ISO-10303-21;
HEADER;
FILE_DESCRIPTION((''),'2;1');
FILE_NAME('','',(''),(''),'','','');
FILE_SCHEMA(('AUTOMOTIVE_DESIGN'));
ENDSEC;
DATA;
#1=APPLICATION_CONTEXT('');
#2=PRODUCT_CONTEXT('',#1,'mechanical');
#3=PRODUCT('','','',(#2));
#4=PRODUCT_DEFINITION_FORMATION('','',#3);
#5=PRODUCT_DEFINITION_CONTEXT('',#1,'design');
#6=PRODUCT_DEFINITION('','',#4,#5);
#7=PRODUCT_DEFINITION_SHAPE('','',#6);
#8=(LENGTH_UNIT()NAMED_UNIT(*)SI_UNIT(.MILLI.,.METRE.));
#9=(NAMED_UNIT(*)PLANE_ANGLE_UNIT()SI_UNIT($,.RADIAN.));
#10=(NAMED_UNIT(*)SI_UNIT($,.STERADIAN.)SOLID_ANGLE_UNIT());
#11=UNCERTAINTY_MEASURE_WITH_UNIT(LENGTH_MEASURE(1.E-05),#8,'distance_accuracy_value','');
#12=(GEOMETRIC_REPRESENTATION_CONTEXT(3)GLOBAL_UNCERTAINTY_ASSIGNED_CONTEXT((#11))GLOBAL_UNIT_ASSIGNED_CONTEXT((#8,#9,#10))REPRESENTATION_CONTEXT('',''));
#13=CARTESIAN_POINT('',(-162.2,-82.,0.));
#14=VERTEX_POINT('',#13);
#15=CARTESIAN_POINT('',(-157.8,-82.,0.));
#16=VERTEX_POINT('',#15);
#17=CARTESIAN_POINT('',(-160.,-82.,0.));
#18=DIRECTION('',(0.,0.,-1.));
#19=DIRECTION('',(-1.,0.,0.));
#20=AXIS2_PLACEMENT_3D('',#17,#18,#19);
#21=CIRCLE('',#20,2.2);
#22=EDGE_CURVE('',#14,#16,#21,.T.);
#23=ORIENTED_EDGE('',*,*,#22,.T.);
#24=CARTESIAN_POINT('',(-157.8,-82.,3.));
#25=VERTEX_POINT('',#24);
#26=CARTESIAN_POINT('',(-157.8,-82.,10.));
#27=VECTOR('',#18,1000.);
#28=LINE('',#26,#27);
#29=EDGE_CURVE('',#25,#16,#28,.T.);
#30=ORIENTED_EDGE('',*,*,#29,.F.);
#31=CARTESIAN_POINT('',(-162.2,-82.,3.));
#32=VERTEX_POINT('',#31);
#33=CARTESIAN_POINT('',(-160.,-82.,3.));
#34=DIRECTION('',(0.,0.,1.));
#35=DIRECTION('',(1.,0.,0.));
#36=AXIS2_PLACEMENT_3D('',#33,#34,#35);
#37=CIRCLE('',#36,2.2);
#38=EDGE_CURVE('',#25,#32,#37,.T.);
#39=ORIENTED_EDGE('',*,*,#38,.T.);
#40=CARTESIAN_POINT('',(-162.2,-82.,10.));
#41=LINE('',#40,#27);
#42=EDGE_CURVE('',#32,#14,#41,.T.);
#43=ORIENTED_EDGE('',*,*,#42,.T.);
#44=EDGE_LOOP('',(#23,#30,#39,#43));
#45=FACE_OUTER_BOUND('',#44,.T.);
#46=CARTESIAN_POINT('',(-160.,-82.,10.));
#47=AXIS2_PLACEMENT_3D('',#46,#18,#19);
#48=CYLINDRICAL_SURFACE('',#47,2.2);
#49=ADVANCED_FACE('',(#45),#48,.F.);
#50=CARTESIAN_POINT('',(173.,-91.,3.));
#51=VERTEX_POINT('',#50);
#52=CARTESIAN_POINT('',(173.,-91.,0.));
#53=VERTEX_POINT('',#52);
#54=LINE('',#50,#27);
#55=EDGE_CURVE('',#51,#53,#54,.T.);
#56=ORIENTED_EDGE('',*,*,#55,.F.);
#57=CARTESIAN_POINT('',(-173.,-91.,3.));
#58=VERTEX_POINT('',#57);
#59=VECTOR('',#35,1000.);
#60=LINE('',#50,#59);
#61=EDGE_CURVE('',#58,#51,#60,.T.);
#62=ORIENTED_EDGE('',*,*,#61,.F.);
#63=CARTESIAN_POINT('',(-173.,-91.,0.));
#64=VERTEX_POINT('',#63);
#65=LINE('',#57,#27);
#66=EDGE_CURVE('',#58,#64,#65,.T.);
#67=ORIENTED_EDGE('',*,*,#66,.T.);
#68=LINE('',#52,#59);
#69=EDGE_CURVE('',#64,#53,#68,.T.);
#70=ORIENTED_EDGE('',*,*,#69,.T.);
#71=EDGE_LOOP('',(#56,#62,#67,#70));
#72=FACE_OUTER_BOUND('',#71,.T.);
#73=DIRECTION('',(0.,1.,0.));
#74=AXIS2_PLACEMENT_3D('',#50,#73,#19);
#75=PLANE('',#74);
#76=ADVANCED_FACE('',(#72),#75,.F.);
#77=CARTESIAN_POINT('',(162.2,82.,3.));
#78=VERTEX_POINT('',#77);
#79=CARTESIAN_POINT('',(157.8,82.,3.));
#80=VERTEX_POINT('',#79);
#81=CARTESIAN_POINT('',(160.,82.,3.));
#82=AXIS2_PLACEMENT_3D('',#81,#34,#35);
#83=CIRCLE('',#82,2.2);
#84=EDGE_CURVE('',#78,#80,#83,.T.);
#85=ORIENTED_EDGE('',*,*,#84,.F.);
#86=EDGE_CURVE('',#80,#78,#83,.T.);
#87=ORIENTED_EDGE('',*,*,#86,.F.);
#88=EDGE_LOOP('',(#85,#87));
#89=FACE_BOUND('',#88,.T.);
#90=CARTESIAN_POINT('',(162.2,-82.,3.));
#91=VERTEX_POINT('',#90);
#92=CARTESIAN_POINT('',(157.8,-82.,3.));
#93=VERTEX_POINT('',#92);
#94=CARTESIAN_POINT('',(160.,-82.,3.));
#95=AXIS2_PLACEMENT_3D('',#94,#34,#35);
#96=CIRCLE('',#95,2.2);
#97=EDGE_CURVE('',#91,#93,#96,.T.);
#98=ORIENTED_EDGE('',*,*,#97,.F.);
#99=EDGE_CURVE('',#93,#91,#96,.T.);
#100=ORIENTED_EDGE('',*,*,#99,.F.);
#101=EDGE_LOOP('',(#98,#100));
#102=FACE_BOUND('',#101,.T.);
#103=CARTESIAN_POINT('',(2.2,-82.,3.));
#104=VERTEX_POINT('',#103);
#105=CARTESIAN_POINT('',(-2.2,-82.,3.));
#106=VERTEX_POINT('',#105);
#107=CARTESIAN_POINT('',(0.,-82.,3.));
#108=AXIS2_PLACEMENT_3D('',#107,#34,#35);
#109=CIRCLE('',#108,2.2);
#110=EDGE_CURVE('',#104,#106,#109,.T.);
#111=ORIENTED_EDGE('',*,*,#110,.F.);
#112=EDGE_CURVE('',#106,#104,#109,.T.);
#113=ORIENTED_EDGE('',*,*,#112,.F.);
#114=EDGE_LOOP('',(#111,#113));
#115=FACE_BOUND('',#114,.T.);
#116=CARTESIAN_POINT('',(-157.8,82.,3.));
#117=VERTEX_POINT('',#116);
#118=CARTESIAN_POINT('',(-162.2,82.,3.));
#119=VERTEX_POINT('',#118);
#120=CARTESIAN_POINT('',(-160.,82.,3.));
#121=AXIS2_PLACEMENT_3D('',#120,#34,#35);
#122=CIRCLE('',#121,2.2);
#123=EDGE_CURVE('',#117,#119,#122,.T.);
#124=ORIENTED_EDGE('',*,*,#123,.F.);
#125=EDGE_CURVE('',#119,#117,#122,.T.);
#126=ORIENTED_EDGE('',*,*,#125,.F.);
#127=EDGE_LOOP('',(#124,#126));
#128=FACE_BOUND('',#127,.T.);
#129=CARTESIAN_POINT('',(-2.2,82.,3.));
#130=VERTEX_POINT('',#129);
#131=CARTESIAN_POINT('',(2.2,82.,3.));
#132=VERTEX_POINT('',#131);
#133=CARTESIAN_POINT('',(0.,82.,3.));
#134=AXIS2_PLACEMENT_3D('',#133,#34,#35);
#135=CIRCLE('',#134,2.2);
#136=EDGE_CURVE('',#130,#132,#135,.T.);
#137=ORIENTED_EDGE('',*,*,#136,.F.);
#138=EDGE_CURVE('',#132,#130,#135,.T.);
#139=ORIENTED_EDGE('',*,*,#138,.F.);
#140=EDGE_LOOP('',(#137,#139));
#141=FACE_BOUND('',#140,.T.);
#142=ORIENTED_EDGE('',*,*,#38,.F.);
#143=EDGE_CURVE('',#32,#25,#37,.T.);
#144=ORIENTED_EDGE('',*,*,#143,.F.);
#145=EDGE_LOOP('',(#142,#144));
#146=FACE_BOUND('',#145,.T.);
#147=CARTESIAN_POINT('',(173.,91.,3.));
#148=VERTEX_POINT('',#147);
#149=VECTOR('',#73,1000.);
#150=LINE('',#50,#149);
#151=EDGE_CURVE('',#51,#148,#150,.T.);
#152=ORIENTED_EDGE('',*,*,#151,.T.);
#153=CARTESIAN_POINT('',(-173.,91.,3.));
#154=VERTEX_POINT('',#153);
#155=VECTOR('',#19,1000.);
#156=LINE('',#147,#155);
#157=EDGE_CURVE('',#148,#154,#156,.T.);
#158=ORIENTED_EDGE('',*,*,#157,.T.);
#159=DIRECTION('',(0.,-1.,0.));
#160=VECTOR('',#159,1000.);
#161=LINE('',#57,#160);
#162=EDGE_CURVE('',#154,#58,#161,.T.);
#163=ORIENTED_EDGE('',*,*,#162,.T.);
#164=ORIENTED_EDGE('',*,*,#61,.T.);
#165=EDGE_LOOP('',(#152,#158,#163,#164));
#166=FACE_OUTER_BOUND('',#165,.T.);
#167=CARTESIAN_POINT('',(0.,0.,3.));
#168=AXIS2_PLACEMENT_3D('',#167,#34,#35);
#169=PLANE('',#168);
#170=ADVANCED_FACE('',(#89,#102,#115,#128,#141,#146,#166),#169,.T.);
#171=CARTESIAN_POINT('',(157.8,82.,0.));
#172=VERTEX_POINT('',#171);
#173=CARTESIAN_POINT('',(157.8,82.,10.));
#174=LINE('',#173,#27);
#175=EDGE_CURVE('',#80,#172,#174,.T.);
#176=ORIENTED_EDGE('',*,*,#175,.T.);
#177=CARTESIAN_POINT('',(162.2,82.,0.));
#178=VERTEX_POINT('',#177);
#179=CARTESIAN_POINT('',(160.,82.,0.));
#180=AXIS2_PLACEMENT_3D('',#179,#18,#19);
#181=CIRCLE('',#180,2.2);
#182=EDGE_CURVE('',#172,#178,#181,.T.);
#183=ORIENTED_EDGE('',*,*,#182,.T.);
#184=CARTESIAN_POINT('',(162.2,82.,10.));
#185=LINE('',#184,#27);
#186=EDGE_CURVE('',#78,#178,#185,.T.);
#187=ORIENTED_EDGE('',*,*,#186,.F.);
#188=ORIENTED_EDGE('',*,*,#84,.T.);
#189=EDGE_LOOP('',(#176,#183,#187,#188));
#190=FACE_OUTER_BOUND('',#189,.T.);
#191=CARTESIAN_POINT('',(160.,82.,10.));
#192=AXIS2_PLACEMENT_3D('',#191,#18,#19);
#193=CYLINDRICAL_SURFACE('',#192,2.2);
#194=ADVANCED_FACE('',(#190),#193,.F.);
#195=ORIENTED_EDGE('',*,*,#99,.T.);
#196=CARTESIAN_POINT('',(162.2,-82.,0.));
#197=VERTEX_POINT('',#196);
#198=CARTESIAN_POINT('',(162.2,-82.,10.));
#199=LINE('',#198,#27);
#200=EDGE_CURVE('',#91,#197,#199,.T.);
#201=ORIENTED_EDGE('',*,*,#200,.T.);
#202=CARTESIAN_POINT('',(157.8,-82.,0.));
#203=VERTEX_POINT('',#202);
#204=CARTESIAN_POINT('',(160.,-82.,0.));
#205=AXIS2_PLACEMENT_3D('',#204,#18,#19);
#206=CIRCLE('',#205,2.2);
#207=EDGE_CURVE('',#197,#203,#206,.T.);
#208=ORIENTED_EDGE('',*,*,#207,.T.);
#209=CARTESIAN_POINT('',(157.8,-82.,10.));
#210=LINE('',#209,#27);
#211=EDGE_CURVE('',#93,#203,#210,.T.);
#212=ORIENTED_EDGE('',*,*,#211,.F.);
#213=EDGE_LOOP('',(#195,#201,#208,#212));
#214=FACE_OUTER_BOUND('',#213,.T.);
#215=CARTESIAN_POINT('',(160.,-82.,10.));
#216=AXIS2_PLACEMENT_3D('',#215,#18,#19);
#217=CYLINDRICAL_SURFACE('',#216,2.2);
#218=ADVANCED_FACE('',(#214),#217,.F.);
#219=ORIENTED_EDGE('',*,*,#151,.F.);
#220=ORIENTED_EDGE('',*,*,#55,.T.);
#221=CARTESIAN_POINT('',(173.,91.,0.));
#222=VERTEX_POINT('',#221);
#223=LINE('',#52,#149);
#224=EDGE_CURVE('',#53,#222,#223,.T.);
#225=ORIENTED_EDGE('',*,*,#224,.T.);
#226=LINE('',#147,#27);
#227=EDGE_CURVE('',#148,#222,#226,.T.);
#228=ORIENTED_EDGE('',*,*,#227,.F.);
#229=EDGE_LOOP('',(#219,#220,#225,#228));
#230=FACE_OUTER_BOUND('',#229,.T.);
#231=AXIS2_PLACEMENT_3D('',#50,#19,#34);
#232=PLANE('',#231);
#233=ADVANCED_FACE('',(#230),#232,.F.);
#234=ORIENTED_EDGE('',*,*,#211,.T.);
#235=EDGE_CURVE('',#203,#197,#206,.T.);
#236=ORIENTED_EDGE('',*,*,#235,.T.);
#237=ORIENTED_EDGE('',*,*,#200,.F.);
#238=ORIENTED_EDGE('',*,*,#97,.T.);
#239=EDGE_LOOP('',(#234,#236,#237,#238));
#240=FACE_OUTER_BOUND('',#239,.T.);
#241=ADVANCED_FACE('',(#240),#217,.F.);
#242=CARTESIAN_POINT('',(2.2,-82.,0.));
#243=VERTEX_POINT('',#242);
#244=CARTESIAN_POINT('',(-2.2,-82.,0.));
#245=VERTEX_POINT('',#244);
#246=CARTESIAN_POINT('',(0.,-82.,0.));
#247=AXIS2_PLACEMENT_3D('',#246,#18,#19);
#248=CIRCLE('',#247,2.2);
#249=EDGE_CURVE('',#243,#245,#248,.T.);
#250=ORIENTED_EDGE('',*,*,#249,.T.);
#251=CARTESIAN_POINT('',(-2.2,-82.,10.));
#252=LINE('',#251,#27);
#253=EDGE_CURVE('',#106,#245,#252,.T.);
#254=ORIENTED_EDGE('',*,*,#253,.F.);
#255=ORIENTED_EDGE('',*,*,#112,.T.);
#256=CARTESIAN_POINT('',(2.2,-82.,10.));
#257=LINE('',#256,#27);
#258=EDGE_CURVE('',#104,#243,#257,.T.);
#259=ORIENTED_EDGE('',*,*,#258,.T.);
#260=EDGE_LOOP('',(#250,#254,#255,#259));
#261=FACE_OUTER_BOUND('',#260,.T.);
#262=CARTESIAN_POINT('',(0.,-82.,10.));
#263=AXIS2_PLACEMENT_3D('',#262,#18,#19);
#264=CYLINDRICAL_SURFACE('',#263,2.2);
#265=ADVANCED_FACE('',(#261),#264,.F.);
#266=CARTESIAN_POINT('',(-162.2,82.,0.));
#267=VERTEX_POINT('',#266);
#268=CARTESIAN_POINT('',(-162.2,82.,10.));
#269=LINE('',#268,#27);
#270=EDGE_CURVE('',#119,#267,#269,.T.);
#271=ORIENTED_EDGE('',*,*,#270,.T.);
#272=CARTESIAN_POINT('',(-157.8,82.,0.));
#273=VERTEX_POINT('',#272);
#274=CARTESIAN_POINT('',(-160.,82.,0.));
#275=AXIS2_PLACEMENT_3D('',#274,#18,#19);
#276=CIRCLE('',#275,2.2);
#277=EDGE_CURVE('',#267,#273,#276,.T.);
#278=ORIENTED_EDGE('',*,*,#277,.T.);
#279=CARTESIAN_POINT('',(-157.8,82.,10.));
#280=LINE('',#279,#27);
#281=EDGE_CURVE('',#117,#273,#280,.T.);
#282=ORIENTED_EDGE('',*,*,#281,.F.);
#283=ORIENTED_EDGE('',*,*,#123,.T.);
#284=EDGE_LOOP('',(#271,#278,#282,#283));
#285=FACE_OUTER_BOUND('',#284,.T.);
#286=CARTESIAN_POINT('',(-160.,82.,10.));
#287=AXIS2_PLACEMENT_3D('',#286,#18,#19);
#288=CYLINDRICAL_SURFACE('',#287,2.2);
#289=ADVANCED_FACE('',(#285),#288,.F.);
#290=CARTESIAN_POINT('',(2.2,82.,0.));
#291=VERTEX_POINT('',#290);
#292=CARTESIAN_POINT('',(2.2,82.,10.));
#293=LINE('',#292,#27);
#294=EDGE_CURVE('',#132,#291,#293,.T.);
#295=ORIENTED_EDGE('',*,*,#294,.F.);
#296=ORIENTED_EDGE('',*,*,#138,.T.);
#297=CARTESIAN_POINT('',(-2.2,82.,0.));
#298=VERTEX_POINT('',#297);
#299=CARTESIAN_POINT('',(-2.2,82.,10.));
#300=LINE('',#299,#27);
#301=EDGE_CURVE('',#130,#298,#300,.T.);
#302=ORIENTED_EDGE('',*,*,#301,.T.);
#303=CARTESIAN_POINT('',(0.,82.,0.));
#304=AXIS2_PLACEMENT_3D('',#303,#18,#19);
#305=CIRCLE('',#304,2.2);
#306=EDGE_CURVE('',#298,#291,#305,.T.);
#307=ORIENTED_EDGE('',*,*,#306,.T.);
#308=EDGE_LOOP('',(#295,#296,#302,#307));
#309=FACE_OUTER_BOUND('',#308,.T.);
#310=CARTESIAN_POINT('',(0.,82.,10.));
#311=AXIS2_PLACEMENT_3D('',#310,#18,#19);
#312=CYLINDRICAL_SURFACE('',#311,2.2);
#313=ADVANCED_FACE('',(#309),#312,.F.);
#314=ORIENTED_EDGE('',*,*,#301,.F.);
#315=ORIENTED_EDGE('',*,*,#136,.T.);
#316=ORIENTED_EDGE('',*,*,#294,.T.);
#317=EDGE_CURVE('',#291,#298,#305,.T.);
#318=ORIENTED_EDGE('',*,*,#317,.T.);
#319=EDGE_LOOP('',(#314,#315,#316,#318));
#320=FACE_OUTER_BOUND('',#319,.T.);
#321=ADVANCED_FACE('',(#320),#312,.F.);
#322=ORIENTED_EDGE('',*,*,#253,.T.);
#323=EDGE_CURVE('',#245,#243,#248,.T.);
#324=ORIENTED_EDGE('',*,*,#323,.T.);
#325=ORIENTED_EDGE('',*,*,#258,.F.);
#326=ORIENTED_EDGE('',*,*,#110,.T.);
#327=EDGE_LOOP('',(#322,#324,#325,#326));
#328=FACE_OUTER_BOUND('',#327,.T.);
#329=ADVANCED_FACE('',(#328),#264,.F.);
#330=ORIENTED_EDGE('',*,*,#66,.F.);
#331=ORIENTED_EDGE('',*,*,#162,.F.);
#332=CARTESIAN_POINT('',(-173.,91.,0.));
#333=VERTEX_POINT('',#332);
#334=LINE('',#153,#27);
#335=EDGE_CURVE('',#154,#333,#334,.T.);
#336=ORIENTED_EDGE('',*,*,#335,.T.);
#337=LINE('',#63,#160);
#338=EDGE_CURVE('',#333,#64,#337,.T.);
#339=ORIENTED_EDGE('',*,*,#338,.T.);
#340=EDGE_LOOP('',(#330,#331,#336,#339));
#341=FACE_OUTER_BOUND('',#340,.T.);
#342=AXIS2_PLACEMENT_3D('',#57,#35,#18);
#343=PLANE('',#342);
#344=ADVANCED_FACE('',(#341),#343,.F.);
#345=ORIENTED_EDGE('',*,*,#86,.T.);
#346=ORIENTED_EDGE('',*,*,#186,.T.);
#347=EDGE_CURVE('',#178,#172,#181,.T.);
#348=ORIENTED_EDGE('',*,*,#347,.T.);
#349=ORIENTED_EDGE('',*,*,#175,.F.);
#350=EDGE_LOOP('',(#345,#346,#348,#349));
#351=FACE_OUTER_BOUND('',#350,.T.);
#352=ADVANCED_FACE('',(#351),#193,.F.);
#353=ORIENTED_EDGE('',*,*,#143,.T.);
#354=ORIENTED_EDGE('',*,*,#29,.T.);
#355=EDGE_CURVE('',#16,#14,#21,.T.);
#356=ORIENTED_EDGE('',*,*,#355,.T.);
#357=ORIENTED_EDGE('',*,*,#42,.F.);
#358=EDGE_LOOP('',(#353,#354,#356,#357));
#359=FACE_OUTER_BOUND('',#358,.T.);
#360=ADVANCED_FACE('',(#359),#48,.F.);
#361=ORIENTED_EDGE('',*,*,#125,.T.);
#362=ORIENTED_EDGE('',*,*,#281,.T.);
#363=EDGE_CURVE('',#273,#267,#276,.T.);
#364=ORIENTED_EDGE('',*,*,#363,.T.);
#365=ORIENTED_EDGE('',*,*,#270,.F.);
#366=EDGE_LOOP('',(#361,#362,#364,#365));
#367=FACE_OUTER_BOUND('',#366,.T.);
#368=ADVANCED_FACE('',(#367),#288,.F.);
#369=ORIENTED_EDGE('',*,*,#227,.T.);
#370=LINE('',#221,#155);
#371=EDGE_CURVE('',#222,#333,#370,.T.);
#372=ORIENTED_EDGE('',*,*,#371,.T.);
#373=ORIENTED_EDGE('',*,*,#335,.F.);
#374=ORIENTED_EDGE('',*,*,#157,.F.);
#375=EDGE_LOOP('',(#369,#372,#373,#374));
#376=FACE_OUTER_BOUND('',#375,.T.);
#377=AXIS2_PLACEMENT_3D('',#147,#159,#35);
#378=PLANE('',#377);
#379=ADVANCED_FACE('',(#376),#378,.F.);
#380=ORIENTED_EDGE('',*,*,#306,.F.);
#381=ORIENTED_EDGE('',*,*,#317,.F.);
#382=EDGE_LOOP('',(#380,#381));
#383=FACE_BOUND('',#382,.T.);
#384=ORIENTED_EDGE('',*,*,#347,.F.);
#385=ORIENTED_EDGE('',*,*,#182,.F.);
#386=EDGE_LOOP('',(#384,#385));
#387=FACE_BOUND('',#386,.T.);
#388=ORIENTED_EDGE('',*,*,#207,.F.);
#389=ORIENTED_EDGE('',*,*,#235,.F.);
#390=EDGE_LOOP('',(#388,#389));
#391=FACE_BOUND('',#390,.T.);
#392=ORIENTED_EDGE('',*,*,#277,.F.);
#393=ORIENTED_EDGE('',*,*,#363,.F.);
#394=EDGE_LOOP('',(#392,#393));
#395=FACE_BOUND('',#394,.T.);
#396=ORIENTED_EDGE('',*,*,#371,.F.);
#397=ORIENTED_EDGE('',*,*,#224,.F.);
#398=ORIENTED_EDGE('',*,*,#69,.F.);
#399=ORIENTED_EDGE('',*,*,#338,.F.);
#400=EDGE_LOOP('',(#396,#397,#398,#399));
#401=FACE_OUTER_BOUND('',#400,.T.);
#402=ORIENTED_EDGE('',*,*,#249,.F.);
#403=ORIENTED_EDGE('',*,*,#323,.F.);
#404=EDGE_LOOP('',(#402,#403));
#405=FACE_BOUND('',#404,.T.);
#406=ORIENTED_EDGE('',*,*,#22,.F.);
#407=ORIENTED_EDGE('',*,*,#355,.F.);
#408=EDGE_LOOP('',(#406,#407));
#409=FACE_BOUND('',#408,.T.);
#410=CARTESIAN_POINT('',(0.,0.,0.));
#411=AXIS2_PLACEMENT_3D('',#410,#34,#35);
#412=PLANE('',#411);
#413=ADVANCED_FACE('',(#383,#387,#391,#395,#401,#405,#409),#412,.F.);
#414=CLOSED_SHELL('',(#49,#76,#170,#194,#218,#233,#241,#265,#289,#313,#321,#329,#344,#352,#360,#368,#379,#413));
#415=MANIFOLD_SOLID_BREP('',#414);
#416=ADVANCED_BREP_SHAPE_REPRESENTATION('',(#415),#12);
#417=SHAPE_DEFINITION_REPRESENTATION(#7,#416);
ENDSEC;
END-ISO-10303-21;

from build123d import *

# Parameters (mm, degrees)
SKETCH_1_W          = 346
SKETCH_1_H          = 182
EXTRUDE_1_DEPTH     = 3
SKETCH_2_R          = 2.2
CUT_EXTRUDE_1_DEPTH = 10


with BuildPart() as part:
    # 草图1 → 凸台-拉伸1 (new body)
    with BuildSketch(Plane.XY):
        Rectangle(SKETCH_1_W, SKETCH_1_H)
    extrude(amount=EXTRUDE_1_DEPTH)

    # 草图2 → 切除-拉伸1 (cut)
    with BuildSketch(Plane(origin=(0, 0, 0), x_dir=(-1, 0, 0), z_dir=(0, 0, -1))):
        with Locations((0, 82)):
            Circle(SKETCH_2_R)
        with Locations((160, 82)):
            Circle(SKETCH_2_R)
        with Locations((0, -82)):
            Circle(SKETCH_2_R)
        with Locations((160, -82)):
            Circle(SKETCH_2_R)
        with Locations((-160, -82)):
            Circle(SKETCH_2_R)
        with Locations((-160, 82)):
            Circle(SKETCH_2_R)
    extrude(amount=-CUT_EXTRUDE_1_DEPTH, mode=Mode.SUBTRACT)


solid = part.part
